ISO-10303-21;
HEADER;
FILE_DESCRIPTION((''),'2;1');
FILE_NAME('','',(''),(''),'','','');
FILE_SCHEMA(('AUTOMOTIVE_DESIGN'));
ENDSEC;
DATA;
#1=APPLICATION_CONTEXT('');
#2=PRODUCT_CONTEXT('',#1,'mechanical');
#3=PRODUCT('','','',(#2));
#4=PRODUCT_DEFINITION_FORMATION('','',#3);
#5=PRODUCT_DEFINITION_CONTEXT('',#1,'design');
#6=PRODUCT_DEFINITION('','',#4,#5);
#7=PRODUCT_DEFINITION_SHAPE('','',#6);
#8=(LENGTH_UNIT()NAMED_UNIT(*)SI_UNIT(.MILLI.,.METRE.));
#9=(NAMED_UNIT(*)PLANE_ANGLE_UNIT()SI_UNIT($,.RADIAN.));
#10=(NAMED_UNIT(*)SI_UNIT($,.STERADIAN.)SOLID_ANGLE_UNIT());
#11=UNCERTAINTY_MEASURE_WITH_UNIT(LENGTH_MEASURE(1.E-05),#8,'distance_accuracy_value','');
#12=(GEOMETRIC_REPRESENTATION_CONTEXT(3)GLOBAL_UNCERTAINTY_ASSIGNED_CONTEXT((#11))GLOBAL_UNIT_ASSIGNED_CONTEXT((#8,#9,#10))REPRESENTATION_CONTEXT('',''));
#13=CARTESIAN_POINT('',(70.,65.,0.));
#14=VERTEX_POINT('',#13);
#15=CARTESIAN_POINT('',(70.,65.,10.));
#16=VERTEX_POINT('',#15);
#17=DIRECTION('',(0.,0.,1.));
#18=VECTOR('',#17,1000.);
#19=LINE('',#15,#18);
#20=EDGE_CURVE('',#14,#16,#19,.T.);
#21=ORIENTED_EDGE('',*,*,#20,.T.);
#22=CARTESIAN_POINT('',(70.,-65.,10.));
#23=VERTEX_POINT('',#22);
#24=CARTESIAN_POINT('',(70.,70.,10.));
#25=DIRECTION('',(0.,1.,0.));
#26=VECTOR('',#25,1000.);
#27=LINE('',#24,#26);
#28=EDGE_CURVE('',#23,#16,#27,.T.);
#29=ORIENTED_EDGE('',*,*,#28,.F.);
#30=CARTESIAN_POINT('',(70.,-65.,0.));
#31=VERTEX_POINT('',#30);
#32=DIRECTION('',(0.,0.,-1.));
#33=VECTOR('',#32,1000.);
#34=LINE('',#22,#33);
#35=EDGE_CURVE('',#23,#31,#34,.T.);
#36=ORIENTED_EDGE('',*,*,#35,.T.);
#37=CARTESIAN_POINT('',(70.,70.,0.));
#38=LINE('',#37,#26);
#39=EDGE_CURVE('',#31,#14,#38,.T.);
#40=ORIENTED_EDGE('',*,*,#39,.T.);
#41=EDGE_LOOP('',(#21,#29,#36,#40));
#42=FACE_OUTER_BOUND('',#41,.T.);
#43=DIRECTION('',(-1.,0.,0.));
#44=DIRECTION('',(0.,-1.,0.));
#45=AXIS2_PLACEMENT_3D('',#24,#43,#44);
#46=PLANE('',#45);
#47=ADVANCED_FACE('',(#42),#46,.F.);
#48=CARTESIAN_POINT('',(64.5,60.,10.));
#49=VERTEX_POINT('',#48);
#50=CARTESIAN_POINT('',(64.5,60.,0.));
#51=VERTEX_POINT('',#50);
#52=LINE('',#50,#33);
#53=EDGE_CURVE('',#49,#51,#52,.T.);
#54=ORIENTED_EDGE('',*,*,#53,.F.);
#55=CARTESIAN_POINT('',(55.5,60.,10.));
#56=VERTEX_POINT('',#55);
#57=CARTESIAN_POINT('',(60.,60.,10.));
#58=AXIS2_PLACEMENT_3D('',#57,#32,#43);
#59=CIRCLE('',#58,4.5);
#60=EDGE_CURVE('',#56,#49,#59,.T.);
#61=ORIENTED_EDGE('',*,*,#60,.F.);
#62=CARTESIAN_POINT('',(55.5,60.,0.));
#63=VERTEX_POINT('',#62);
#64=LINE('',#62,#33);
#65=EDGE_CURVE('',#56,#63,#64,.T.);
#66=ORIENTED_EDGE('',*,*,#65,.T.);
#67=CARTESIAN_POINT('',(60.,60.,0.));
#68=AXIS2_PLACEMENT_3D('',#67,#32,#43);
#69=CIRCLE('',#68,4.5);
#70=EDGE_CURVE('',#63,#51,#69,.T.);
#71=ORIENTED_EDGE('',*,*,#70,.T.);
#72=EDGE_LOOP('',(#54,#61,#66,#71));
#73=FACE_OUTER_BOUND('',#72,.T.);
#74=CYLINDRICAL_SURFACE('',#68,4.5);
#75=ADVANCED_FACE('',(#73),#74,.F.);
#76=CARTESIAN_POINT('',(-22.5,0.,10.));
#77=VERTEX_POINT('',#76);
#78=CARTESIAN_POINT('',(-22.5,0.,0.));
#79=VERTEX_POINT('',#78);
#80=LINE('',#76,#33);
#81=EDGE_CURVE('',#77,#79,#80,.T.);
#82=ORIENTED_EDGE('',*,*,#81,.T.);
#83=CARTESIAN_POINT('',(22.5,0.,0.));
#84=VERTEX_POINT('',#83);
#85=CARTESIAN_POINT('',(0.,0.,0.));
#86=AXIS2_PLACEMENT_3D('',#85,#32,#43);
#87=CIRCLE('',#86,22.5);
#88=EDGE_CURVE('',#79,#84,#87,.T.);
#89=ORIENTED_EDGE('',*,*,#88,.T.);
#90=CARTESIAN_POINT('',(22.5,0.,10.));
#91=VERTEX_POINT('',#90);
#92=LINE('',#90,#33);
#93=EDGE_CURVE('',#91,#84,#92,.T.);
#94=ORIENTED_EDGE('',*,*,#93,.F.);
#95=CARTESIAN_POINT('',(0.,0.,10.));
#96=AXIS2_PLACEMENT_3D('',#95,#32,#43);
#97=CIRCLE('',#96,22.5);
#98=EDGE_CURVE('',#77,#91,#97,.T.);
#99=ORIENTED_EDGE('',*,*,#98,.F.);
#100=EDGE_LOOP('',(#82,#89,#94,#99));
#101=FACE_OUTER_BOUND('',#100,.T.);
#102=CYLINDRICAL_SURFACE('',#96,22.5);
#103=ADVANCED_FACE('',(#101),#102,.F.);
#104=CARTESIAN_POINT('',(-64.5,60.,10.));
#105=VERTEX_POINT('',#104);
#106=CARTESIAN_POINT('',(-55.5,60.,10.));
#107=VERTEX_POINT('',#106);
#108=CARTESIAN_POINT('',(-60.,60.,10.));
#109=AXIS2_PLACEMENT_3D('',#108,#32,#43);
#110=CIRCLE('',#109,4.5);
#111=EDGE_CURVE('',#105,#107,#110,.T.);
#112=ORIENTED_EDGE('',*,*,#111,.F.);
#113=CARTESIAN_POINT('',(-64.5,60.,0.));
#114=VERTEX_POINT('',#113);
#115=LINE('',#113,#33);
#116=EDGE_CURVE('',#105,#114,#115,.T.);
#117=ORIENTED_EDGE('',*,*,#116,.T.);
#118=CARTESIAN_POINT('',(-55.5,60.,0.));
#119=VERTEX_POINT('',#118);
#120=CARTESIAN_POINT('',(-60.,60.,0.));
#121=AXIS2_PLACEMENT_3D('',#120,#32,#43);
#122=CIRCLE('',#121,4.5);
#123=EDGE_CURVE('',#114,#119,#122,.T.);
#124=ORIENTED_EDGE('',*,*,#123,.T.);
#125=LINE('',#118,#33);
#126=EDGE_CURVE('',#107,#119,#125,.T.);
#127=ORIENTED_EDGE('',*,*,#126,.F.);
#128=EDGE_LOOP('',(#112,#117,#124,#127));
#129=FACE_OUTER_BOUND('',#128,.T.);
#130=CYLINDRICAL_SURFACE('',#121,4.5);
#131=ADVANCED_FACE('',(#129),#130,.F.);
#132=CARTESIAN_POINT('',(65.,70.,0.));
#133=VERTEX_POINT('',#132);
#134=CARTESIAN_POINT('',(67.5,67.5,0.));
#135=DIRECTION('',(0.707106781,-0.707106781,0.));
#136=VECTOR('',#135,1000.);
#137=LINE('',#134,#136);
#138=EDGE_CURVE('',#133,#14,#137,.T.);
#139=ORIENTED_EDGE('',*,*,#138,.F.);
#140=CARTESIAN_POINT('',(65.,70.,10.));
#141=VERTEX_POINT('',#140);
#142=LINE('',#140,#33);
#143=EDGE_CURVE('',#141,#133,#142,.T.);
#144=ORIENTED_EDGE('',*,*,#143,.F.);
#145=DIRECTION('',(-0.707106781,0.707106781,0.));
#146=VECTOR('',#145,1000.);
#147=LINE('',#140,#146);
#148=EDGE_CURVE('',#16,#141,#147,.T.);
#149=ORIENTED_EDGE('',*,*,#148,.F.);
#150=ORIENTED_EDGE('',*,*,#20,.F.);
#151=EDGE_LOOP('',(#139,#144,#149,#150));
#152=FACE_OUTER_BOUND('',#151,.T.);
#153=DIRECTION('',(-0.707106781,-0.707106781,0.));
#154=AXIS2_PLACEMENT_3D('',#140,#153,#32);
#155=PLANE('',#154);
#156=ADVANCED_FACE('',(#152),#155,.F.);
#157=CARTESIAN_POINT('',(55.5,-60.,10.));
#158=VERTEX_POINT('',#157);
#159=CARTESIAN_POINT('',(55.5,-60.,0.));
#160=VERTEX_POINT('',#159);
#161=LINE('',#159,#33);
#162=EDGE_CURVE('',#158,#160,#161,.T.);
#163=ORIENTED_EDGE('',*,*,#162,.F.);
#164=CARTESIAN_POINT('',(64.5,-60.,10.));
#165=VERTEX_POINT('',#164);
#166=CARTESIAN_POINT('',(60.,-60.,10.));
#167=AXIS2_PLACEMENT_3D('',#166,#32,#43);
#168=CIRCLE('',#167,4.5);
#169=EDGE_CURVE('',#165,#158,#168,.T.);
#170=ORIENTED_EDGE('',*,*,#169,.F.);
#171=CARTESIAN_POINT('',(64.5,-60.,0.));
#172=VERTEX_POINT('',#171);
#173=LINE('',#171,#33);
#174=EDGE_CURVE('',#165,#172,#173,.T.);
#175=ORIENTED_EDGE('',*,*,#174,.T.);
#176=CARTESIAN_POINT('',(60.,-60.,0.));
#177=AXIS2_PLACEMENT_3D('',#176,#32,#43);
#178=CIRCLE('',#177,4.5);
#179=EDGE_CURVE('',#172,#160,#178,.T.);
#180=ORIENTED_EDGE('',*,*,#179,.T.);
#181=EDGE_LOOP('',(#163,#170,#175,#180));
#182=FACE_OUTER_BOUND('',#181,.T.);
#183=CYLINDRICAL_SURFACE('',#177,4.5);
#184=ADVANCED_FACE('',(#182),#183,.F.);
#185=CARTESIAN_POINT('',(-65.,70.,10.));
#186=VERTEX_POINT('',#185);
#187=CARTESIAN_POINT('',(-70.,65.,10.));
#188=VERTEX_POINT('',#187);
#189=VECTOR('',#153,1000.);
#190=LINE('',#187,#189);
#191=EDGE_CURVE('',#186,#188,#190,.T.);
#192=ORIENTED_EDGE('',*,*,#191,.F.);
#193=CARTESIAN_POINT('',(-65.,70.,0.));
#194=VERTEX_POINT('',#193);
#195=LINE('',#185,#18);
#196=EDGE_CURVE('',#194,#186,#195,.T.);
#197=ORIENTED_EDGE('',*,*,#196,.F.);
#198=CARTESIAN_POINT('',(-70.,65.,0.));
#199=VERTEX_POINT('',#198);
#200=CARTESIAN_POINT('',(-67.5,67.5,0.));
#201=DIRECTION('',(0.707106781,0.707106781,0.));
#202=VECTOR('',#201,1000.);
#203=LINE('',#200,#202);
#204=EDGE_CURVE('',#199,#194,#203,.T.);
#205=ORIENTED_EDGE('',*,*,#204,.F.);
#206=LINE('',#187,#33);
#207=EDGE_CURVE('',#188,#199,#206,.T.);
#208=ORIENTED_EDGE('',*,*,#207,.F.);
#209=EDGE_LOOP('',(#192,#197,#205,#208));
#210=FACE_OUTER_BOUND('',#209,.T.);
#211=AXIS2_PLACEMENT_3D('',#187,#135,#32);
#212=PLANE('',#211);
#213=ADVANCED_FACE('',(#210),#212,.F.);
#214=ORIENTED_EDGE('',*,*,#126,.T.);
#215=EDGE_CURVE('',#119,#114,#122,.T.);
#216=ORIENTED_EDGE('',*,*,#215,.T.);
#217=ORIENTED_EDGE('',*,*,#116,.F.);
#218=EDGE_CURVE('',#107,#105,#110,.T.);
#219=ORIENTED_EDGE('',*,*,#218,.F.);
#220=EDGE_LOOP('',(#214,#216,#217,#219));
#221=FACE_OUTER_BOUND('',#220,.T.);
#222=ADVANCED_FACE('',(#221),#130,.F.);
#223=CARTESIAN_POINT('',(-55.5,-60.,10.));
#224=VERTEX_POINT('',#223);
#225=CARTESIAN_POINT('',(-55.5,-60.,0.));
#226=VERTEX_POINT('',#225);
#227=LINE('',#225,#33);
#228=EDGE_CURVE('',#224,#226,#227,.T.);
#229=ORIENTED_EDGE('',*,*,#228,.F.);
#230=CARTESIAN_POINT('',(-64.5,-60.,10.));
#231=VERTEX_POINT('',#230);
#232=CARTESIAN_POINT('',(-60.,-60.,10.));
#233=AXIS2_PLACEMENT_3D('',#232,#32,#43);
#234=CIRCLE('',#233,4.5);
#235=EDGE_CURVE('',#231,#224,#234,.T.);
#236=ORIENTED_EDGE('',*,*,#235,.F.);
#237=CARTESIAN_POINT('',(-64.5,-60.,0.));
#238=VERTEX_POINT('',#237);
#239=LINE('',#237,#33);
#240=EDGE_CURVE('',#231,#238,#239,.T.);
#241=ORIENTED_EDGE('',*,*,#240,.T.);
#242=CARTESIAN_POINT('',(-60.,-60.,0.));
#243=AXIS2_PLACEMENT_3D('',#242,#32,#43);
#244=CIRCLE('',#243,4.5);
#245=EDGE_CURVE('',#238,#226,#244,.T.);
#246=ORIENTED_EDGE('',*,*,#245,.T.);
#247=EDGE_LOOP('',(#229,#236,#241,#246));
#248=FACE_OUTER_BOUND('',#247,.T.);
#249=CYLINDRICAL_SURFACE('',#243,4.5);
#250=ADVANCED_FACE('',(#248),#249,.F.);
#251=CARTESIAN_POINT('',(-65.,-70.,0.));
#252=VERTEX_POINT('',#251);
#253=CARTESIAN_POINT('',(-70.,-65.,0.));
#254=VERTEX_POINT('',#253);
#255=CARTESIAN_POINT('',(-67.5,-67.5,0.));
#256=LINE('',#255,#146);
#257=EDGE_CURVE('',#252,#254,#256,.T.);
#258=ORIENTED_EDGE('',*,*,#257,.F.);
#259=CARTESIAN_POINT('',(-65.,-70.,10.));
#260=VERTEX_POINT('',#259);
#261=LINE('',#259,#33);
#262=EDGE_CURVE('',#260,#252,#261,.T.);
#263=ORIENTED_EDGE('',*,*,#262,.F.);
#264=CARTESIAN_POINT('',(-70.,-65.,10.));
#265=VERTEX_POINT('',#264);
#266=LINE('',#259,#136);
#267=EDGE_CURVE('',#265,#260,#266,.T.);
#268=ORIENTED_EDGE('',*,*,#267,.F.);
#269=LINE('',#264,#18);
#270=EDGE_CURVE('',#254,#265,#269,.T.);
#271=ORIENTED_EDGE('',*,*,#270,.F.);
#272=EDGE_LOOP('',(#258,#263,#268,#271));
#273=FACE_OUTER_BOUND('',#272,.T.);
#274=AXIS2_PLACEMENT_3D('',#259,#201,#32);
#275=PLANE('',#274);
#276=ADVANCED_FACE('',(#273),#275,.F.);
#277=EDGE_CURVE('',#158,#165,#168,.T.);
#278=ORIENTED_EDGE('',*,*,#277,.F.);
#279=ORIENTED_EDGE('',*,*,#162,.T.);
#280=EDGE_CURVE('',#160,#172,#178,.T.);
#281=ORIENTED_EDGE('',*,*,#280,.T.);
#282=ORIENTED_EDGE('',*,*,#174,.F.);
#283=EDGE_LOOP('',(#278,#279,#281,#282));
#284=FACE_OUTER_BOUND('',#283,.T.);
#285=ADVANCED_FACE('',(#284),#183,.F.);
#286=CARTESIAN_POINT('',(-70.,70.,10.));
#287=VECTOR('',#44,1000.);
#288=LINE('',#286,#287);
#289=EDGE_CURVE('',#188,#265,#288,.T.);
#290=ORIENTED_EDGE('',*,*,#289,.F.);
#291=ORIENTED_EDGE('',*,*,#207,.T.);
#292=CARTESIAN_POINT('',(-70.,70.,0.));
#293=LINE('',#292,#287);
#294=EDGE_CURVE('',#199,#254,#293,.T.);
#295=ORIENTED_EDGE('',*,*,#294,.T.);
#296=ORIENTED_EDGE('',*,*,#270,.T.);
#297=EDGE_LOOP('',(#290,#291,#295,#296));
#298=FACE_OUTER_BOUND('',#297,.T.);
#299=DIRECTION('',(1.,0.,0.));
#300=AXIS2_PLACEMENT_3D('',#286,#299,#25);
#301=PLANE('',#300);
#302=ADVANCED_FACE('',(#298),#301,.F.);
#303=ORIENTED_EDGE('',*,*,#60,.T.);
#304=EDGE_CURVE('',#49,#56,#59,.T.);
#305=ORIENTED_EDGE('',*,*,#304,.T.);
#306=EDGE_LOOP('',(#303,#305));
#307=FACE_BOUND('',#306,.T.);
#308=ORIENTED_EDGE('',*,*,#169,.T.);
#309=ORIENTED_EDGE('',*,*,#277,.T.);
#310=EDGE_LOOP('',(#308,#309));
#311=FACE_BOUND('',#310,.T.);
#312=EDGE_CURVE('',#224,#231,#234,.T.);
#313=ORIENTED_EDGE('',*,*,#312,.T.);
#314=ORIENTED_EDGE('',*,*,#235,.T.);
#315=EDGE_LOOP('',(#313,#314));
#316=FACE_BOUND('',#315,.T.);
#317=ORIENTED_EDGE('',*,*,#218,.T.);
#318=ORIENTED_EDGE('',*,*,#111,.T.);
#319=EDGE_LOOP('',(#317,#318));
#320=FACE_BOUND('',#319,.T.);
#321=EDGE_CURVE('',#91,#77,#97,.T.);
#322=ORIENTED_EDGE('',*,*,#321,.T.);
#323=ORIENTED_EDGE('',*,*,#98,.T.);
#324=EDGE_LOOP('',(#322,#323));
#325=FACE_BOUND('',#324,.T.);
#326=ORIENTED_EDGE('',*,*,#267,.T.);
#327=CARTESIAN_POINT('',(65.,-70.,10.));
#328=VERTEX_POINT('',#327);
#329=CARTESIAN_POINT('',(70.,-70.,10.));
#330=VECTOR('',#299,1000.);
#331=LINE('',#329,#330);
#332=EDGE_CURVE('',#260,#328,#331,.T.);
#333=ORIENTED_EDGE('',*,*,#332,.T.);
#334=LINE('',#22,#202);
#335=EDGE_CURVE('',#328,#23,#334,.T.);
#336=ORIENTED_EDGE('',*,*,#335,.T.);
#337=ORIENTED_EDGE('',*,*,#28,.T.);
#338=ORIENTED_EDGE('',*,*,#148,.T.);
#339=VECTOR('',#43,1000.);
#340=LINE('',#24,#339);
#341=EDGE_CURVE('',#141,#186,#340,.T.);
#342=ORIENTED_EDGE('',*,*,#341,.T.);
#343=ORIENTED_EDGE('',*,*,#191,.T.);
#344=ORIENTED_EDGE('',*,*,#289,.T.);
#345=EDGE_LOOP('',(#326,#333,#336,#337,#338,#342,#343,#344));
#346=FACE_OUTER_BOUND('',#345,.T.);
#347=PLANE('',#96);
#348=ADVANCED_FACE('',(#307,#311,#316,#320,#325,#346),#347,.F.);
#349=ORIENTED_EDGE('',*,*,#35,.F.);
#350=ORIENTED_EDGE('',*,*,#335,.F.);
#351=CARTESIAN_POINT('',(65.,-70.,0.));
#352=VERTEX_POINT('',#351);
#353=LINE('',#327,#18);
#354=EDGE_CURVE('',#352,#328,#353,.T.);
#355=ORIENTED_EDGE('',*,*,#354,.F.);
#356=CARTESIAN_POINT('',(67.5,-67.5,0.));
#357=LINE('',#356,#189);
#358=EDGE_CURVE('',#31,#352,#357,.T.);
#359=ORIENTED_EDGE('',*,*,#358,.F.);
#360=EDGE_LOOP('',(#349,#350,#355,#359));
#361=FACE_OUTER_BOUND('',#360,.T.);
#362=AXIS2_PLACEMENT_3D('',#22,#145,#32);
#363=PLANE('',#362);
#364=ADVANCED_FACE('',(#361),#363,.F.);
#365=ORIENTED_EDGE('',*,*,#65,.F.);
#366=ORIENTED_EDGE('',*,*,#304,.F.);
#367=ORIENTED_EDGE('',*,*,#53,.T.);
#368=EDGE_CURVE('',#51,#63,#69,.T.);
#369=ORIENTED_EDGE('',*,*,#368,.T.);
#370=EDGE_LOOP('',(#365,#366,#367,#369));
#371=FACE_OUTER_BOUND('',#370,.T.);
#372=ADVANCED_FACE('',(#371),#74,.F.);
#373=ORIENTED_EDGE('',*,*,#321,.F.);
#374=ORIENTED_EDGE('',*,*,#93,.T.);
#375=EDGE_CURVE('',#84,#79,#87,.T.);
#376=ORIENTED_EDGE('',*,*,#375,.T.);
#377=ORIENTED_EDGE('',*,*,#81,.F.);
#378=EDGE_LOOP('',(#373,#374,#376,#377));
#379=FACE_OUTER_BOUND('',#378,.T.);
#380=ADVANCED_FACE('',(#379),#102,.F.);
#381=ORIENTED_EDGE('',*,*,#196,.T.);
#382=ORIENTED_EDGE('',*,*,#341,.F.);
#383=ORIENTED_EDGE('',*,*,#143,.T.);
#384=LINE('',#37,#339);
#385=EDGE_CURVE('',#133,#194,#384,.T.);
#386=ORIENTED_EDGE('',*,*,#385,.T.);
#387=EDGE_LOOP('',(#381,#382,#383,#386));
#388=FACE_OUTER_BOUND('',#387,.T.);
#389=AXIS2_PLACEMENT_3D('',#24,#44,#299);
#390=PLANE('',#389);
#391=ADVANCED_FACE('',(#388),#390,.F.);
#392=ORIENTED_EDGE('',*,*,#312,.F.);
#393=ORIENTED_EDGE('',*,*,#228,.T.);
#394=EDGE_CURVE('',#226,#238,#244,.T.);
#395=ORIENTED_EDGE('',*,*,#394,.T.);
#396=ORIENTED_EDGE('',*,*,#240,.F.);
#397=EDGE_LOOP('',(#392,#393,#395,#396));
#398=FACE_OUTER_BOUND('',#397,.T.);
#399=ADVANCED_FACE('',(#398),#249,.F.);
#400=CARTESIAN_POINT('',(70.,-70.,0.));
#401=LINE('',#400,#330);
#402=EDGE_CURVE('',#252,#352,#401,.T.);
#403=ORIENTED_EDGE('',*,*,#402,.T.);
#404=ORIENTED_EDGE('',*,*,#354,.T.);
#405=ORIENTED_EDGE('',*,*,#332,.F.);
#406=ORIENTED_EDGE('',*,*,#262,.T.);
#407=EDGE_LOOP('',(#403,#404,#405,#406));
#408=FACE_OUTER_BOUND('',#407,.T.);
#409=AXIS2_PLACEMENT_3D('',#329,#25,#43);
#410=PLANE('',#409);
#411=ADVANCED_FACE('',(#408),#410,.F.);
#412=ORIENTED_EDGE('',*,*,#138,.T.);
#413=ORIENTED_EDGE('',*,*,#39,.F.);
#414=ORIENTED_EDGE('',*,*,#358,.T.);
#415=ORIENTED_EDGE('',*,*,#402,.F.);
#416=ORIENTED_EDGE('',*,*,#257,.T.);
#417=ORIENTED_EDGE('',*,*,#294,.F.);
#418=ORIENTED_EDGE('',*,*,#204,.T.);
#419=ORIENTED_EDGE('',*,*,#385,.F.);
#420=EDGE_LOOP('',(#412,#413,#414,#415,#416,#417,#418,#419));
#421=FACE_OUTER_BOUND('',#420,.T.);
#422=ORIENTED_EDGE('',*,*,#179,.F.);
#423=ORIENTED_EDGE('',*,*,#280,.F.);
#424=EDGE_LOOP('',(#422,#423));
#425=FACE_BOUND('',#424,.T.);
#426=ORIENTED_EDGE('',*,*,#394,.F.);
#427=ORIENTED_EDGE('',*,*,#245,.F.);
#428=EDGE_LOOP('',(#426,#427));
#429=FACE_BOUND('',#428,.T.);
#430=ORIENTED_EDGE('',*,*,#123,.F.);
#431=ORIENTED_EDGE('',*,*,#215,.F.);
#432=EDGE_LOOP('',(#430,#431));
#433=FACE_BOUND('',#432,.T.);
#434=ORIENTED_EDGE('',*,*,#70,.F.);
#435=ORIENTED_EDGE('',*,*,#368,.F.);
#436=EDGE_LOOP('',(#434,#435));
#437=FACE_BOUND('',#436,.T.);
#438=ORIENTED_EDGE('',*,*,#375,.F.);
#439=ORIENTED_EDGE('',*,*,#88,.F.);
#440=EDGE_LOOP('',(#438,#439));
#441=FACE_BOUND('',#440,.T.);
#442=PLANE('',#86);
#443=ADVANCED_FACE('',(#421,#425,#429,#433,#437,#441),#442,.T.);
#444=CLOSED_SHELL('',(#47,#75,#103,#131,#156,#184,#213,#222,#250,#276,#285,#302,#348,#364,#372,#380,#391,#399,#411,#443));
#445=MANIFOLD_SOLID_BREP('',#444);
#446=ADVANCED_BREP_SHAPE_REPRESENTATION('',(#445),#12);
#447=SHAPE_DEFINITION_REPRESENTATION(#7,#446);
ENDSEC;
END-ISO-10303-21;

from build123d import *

# Parameters (mm, degrees)
SKETCH1_W            = 140
SKETCH1_H            = 140
BOSS_EXTRUDE1_DEPTH  = 10
CHAMFER1_SIZE        = 5
LPATTERN1_COUNT      = 2
LPATTERN1_PITCH      = 120
LPATTERN1_COUNT_DIR2 = 2
LPATTERN1_PITCH_DIR2 = 120
SKETCH4_R            = 22.5
CUT_EXTRUDE1_DEPTH   = 10


with BuildPart() as part:
    # Sketch1 → Boss-Extrude1 (new body)
    with BuildSketch(Plane.XY):
        Rectangle(SKETCH1_W, SKETCH1_H)
    extrude(amount=BOSS_EXTRUDE1_DEPTH)

    # Chamfer1
    chamfer1_edges = [part.edges().sort_by_distance(p)[0] for p in [
        (-70, 70, 5),
        (70, 70, 5),
        (70, -70, 5),
        (-70, -70, 5),
    ]]
    chamfer(chamfer1_edges, length=CHAMFER1_SIZE)

    # Sketch3 → Ø9.0 (9) Diameter Hole1 (revolve, cut)
    with BuildSketch(Plane(origin=(60, -60, 0), x_dir=(0, 1, 0), z_dir=(1, 0, 0))):
        Polygon((0, 0), (0, 22.453872786), (4.5, 19.75), (4.5, 0), align=None)
    f_9_0_9_diameter_hole1 = revolve(axis=Axis((60, -60, -6.35), (0, 0, 1)), mode=Mode.SUBTRACT)

    # LPattern1: 9.0 _9_ Diameter Hole1 2 × 2
    with Locations(*[(-j * LPATTERN1_PITCH_DIR2, i * LPATTERN1_PITCH, 0) for i in range(LPATTERN1_COUNT) for j in range(LPATTERN1_COUNT_DIR2) if (i, j) != (0, 0)]):
        add(f_9_0_9_diameter_hole1, mode=Mode.SUBTRACT)

    # Sketch4 → Cut-Extrude1 (cut)
    with BuildSketch(Plane(origin=(0, 0, 0), x_dir=(-1, 0, 0), z_dir=(0, 0, -1))):
        Circle(SKETCH4_R)
    extrude(amount=-CUT_EXTRUDE1_DEPTH, mode=Mode.SUBTRACT)


solid = part.part
